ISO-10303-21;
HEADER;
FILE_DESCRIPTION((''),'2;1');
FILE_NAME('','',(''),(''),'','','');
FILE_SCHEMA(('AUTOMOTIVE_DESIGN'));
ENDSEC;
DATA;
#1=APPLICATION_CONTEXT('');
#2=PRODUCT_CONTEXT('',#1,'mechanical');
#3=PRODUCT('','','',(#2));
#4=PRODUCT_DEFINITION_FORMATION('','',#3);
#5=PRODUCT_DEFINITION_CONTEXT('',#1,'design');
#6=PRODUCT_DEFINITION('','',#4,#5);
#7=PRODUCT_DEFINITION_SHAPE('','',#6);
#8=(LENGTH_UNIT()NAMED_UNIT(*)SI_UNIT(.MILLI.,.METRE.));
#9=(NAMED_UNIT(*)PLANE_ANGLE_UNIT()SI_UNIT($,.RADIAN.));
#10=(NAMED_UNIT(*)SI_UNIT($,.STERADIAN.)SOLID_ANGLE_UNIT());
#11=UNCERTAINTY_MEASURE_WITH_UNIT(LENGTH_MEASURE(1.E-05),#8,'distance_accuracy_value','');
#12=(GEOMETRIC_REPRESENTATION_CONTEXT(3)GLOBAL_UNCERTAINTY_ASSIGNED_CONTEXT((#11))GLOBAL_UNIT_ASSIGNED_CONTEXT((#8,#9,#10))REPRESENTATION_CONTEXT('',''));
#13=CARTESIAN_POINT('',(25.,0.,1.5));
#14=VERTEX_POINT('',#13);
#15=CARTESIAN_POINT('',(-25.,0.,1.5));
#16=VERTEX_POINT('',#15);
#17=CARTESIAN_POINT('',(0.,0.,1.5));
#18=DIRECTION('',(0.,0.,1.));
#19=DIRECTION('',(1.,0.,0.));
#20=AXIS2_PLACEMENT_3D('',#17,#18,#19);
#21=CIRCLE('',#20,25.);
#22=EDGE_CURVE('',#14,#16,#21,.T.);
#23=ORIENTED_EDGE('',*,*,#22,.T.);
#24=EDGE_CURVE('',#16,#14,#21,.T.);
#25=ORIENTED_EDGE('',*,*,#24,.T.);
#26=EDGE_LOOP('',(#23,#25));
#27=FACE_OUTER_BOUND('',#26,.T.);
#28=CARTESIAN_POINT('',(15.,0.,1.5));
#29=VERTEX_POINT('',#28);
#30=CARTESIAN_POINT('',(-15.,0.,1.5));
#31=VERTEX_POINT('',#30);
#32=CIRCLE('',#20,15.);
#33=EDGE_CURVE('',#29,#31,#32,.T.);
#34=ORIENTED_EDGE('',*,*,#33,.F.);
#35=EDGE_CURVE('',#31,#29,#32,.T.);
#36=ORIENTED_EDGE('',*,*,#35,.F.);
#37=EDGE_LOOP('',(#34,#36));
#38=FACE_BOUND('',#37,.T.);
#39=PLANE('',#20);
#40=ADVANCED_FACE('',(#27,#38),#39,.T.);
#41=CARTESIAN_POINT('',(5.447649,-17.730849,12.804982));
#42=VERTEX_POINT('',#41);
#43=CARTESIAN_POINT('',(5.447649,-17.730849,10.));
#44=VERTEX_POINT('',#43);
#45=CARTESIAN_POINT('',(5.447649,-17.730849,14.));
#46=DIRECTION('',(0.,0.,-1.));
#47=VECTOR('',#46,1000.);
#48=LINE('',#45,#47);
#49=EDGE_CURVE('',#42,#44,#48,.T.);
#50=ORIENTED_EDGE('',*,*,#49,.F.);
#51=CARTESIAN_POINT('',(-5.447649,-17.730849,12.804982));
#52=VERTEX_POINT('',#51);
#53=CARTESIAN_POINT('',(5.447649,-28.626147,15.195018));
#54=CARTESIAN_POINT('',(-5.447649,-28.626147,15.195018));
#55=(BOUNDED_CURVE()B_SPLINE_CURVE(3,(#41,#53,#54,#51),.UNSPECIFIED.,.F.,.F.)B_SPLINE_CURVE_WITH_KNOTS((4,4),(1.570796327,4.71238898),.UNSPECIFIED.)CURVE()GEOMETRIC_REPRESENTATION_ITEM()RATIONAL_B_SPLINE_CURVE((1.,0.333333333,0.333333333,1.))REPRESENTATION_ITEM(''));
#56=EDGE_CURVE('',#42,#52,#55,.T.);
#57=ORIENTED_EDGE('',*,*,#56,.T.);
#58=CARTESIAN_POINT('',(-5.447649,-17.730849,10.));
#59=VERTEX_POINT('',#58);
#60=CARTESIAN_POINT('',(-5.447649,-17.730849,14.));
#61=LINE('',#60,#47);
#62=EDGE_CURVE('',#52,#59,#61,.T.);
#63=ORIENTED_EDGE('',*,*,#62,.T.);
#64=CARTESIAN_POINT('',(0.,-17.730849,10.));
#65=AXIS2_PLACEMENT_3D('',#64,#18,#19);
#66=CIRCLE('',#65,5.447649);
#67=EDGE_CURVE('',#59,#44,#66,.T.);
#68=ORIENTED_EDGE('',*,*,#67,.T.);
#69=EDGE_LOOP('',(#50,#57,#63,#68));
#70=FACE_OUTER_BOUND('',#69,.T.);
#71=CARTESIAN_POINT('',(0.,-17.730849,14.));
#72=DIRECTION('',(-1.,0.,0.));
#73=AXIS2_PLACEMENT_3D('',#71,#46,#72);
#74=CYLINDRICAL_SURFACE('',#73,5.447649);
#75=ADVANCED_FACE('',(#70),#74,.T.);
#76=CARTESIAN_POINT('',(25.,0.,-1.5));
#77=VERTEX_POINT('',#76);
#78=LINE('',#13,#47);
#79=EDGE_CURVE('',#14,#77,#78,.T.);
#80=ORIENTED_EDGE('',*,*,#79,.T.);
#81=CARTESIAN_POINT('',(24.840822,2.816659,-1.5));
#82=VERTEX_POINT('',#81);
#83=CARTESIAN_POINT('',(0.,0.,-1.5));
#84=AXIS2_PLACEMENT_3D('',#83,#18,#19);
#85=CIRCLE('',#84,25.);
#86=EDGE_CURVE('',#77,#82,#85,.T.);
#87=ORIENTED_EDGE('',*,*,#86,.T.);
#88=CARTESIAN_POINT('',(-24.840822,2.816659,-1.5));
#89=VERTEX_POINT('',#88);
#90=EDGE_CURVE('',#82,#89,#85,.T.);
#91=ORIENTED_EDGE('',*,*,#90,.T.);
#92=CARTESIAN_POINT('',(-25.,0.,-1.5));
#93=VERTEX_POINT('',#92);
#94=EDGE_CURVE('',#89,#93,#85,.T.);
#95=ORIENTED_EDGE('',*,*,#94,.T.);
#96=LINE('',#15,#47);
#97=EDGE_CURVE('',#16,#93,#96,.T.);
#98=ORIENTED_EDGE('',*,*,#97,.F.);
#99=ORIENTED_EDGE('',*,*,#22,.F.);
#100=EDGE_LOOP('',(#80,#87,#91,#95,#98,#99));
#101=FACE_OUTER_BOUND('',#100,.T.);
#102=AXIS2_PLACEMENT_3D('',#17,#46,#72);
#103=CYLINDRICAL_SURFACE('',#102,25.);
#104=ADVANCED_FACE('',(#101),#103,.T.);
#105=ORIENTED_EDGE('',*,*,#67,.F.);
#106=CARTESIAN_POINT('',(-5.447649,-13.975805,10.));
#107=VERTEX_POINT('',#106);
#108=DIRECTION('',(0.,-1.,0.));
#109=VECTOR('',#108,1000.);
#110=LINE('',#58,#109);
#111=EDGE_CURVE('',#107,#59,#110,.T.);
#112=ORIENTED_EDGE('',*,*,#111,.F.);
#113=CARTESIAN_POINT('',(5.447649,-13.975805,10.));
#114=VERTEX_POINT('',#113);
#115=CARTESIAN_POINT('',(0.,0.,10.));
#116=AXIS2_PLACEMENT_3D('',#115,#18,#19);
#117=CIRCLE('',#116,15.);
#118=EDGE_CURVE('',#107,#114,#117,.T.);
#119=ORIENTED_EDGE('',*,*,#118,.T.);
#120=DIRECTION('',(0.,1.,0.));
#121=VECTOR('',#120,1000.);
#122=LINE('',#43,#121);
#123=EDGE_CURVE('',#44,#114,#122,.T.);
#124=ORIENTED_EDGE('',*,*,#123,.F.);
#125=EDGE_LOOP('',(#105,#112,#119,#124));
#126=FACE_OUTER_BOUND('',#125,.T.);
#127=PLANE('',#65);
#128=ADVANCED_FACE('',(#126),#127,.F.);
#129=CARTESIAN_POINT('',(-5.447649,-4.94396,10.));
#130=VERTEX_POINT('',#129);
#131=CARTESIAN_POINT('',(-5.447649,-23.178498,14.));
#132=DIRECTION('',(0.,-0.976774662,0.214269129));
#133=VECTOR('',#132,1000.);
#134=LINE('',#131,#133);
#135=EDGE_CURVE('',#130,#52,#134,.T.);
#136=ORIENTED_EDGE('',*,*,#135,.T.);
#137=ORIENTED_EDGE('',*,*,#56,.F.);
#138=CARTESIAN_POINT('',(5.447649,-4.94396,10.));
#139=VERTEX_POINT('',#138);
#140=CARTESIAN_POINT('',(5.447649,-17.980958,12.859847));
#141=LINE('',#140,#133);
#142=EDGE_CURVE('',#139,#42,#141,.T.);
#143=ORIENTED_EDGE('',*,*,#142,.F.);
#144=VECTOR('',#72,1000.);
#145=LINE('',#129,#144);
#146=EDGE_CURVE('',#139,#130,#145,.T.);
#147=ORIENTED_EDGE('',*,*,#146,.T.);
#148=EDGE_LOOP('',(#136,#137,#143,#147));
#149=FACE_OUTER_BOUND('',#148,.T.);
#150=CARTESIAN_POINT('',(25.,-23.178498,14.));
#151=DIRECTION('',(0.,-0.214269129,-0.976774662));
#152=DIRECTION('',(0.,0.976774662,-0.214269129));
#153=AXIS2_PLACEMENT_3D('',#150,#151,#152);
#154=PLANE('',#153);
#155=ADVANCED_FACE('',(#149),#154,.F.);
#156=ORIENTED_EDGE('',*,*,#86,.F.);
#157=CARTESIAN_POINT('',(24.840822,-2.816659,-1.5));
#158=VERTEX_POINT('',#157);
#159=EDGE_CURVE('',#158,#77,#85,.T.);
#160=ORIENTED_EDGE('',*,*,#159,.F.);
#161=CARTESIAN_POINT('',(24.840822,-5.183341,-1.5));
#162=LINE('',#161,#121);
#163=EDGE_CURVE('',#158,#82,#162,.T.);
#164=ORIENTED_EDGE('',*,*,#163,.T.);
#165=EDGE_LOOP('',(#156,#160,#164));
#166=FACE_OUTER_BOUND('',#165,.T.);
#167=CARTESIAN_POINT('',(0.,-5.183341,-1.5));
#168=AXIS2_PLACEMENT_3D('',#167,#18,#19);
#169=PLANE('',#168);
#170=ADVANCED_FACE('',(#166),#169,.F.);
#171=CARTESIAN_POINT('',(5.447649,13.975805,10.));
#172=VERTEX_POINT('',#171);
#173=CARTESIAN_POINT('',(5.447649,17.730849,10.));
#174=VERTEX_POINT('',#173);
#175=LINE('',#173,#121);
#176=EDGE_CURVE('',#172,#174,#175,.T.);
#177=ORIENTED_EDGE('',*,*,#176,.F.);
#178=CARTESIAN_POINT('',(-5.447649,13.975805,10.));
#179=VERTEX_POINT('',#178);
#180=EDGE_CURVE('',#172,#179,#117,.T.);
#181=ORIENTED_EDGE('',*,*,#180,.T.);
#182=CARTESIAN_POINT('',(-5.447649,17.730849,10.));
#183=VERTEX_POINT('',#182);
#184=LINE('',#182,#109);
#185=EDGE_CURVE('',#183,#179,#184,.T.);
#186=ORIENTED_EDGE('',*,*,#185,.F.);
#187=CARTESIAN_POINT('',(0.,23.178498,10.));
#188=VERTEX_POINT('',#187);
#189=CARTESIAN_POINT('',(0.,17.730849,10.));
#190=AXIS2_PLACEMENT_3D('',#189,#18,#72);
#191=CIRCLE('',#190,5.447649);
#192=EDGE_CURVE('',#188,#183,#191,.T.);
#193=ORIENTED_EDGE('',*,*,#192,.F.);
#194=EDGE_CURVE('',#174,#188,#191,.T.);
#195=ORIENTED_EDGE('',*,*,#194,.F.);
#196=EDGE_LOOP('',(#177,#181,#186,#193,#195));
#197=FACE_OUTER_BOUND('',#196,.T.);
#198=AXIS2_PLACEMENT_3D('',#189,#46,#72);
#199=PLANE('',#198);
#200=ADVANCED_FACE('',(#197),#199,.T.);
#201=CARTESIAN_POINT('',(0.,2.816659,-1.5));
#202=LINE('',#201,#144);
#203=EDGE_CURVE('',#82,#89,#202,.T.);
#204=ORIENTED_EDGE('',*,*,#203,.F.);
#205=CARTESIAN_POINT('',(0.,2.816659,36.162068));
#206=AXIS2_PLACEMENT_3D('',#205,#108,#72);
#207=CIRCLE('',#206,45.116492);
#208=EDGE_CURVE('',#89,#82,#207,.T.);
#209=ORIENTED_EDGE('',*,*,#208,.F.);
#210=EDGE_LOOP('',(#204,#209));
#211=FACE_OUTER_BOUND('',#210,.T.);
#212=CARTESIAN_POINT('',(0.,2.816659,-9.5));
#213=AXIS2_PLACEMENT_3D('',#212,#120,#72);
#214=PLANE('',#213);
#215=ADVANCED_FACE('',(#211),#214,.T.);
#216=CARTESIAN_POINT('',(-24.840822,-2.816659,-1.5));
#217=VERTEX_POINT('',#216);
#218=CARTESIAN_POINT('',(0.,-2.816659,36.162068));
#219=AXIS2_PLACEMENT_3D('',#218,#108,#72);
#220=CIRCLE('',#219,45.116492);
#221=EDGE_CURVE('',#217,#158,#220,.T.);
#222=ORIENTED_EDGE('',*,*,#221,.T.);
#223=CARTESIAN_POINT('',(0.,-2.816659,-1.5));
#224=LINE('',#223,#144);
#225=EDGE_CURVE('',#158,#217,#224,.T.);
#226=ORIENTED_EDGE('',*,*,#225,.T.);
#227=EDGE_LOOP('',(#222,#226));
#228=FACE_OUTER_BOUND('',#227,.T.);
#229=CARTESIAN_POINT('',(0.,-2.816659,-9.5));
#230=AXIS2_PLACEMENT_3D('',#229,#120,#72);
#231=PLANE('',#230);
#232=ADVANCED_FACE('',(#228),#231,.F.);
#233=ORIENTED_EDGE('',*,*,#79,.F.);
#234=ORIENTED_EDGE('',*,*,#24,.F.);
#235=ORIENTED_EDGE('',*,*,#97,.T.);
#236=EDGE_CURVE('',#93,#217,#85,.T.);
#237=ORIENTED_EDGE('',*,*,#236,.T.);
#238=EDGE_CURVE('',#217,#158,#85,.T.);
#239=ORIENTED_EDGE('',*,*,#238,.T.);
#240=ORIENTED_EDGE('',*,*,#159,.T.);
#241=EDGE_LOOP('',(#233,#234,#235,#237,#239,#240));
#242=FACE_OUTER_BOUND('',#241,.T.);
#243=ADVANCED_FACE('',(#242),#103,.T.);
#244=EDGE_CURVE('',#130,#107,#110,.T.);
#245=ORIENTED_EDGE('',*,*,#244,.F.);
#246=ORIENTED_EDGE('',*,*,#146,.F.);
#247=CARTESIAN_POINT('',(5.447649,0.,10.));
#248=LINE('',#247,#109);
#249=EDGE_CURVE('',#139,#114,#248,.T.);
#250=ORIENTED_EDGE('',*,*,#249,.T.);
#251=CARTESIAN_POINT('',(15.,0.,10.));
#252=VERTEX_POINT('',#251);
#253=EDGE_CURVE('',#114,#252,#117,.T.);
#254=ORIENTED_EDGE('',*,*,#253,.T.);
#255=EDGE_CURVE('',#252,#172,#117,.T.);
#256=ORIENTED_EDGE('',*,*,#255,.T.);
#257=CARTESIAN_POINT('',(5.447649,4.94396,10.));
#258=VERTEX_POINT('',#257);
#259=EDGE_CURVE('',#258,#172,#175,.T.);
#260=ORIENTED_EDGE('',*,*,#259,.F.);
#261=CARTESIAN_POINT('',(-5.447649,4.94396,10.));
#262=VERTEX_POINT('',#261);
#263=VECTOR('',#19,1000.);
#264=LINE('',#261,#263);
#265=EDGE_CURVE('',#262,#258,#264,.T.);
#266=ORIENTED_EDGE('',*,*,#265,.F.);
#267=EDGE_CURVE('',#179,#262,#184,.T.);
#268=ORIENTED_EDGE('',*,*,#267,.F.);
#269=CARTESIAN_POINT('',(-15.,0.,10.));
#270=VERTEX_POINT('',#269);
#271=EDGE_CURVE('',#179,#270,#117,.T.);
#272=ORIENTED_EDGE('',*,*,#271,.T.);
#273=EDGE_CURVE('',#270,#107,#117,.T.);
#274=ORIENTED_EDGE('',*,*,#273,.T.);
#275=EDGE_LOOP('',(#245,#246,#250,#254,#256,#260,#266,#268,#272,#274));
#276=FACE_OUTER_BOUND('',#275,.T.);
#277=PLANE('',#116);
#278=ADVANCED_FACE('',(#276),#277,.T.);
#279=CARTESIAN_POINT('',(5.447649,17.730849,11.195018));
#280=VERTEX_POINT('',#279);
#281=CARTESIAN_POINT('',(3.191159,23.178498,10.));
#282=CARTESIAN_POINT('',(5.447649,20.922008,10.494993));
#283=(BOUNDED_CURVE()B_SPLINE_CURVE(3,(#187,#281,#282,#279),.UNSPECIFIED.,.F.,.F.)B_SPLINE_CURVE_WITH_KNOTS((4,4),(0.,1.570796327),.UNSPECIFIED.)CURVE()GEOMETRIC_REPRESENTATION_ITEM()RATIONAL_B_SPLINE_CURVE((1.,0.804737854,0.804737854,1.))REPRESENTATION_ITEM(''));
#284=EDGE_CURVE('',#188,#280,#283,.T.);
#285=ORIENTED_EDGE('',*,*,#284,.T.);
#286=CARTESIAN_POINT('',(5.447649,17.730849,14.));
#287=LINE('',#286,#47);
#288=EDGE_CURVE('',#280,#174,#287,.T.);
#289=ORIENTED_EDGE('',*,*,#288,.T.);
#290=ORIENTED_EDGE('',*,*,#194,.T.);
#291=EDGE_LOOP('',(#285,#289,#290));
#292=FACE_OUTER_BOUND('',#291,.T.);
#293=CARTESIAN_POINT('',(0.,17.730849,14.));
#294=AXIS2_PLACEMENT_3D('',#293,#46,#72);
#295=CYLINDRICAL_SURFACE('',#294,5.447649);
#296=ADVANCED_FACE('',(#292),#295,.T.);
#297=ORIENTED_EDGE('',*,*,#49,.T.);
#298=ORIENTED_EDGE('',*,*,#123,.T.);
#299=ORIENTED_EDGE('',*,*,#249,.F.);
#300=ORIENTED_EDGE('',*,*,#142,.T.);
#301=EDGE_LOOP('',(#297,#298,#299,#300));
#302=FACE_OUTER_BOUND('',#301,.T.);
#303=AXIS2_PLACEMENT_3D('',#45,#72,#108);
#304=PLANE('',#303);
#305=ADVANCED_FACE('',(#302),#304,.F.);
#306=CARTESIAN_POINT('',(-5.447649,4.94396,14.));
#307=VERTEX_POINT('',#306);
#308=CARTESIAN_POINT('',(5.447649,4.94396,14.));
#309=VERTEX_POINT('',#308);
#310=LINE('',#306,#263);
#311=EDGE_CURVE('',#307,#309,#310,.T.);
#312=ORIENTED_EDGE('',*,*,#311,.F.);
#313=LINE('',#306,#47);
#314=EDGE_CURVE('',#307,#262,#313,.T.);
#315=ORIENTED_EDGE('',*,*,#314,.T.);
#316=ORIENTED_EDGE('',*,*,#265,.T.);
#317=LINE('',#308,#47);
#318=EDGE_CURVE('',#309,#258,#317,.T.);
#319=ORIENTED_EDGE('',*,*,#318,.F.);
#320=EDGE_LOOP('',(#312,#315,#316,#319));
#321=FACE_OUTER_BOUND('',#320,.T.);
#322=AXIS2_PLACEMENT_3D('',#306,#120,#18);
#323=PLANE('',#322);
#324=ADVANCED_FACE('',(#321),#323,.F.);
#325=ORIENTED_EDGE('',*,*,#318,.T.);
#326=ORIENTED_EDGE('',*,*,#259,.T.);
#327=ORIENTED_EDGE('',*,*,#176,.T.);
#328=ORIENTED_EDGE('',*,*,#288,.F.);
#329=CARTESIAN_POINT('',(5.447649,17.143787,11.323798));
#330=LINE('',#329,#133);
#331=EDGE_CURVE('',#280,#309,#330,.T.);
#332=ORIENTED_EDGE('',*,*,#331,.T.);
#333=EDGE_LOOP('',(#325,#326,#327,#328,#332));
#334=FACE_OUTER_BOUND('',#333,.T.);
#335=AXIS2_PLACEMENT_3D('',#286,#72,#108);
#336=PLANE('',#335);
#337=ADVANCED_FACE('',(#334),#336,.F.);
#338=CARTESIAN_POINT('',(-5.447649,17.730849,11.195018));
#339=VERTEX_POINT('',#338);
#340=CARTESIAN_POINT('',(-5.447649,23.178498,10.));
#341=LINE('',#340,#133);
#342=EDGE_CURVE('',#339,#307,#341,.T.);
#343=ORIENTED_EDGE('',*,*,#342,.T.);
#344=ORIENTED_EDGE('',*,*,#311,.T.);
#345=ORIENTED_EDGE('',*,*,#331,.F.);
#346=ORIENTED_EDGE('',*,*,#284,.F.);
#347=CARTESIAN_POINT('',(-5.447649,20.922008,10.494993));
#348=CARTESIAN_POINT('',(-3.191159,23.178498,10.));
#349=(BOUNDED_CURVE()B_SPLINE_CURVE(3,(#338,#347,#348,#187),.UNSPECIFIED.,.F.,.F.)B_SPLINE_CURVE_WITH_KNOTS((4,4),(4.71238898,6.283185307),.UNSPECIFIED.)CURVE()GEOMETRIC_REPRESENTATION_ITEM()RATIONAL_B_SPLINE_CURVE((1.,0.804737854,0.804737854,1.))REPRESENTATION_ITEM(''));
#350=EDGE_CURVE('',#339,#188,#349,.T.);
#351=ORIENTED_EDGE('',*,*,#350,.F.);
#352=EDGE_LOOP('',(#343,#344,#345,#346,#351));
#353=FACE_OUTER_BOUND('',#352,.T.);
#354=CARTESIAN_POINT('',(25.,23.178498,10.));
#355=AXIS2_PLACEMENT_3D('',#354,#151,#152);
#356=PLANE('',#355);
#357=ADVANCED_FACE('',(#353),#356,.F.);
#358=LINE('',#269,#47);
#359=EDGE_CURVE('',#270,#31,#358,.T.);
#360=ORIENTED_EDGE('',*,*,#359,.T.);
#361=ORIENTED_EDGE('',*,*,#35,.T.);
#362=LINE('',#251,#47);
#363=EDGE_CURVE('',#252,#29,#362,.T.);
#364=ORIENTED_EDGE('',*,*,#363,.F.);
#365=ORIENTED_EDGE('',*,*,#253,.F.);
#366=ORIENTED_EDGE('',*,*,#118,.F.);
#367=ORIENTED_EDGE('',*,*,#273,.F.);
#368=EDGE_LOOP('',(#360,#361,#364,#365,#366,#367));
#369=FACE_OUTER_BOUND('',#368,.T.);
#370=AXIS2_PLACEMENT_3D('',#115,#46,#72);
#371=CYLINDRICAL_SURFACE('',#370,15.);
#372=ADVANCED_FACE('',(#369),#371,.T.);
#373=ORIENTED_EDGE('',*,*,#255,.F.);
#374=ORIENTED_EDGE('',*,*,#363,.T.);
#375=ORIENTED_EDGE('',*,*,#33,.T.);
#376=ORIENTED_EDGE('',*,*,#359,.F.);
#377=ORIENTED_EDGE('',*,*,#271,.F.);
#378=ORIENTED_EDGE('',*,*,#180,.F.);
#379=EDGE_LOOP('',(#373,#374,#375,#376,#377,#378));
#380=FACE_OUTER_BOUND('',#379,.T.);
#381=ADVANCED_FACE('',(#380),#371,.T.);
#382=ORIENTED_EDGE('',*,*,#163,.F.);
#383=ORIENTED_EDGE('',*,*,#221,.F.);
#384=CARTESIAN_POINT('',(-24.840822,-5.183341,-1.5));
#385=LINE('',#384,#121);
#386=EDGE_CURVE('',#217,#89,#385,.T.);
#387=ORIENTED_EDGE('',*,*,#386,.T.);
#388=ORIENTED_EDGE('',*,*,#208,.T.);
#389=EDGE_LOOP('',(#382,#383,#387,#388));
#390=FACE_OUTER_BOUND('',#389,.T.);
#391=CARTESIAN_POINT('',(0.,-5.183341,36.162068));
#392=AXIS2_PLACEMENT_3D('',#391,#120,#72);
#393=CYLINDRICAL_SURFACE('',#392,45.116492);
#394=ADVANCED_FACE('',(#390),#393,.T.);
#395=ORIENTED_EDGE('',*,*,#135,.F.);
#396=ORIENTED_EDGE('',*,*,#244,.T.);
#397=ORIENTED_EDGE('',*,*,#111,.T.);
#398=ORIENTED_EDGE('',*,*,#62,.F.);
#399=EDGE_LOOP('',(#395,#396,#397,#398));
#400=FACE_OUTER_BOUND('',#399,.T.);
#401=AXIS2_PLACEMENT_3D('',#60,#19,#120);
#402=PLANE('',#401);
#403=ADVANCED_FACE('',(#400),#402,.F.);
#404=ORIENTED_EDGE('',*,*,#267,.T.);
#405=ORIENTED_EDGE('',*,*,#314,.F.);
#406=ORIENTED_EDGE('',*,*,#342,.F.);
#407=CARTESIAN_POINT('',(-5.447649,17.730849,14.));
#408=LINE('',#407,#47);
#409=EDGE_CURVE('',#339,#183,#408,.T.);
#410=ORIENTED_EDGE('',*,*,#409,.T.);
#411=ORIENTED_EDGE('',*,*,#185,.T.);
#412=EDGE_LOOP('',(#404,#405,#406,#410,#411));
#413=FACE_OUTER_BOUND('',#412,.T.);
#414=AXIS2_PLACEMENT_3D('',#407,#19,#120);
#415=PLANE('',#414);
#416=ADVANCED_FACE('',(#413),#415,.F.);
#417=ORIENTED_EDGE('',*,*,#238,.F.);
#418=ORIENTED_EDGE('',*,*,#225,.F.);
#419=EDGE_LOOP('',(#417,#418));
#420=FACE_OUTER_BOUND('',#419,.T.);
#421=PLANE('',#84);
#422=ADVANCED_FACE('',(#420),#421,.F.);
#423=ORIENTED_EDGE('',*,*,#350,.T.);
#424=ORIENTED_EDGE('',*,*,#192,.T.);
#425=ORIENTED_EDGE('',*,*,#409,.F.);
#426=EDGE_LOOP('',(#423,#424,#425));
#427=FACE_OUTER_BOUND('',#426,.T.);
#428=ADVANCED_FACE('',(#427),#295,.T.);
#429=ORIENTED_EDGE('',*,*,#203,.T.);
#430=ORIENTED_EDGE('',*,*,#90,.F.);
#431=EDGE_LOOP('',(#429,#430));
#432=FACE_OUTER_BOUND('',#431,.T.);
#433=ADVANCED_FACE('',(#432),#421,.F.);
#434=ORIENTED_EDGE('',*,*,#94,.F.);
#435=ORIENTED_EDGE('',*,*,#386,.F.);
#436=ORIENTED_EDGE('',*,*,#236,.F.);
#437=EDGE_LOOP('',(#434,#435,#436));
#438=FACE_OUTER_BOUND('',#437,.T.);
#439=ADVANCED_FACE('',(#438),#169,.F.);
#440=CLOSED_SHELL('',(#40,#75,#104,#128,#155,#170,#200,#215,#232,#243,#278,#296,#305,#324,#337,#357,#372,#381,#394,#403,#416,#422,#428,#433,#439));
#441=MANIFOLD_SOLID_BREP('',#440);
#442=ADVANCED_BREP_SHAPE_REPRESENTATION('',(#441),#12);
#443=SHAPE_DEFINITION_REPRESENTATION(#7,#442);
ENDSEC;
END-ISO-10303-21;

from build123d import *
from build123d.topology import SkipClean

# Parameters (mm, degrees)
SKETCH1_R           = 25
BOSS_EXTRUDE1_DEPTH = 1.5
BOSS_EXTRUDE2_DEPTH = 8
CUT_EXTRUDE2_DEPTH  = 8
SKETCH4_R           = 15
BOSS_EXTRUDE3_DEPTH = 8.5
BOSS_EXTRUDE4_DEPTH = 4
CUT_EXTRUDE3_DEPTH  = 42.809799474


with BuildPart() as part:
    # Sketch1 → Boss-Extrude1 (new, symmetric)
    with BuildSketch(Plane.XY):
        Circle(SKETCH1_R)
    extrude(amount=BOSS_EXTRUDE1_DEPTH, both=True)

    # Sketch2 → Boss-Extrude2 (add)
    with SkipClean():  # the faces are left unmerged after this step: merging them gives an invalid solid
        with BuildSketch(Plane(origin=(0, 0, -1.5), x_dir=(-1, 0, 0), z_dir=(0, 0, -1))):
            with BuildLine():
                Line((24.840821943, 2.816658516), (-24.840821943, 2.816658516))
                ThreePointArc((-24.840821943, 2.816658516), (-25, 0), (-24.840821943, -2.816658516))
                Line((-24.840821943, -2.816658516), (24.840821943, -2.816658516))
                ThreePointArc((24.840821943, -2.816658516), (24.960173763, -1.410576376), (25, 0))
                ThreePointArc((25, 0), (24.960173763, 1.410576376), (24.840821943, 2.816658516))
            make_face()
        extrude(amount=BOSS_EXTRUDE2_DEPTH)

    # Sketch3 → Cut-Extrude2 (cut)
    with BuildSketch(Plane(origin=(0, 2.816658516, 0), x_dir=(1, 0, 0), z_dir=(0, 1, 0))):
        Polygon((-29.660487574, 11.299873817), (-29.660487574, 1.5), (-24.840821943, 1.5), (-24.840821943, 9.5), (24.840821943, 9.5), (24.840821943, 1.5), (29.900960726, 1.5), (29.900960726, 11.299873817), align=None)
        with BuildLine():
            ThreePointArc((-24.840821943, 1.5), (0, 8.954423408), (24.840821943, 1.5))
            Line((24.840821943, 1.5), (24.840821943, 9.5))
            Line((24.840821943, 9.5), (-24.840821943, 9.5))
            Line((-24.840821943, 9.5), (-24.840821943, 1.5))
        make_face()
    extrude(amount=-CUT_EXTRUDE2_DEPTH, mode=Mode.SUBTRACT)

    # Sketch4 → Boss-Extrude3 (add)
    with BuildSketch(Plane.XY.offset(1.5)):
        Circle(SKETCH4_R)
    extrude(amount=BOSS_EXTRUDE3_DEPTH)

    # Sketch5 → Boss-Extrude4 (add)
    with BuildSketch(Plane.XY.offset(10)):
        with BuildLine():
            Line((-5.44764904, 17.730849129), (-5.44764904, 4.943959841))
            Line((-5.44764904, 4.943959841), (5.44764904, 4.943959841))
            Line((5.44764904, 4.943959841), (5.44764904, 17.730849129))
            ThreePointArc((5.44764904, 17.730849129), (0, 23.17849817), (-5.44764904, 17.730849129))
        make_face()
        with BuildLine():
            Line((-5.44764904, -17.730849129), (-5.44764904, -4.943959841))
            Line((-5.44764904, -4.943959841), (5.44764904, -4.943959841))
            Line((5.44764904, -4.943959841), (5.44764904, -17.730849129))
            ThreePointArc((5.44764904, -17.730849129), (0, -23.17849817), (-5.44764904, -17.730849129))
        make_face()
    extrude(amount=BOSS_EXTRUDE4_DEPTH)

    # Sketch7 → Cut-Extrude3 (cut, through all)
    with BuildSketch(Plane.ZY.offset(5.44764904)):
        Polygon((10, 23.17849817), (14, 4.943959841), (14, 23.17849817), align=None)
        Polygon((14, -23.17849817), (10, -4.943959841), (14, -4.943959841), align=None)
    extrude(amount=-CUT_EXTRUDE3_DEPTH, mode=Mode.SUBTRACT)


solid = part.part
